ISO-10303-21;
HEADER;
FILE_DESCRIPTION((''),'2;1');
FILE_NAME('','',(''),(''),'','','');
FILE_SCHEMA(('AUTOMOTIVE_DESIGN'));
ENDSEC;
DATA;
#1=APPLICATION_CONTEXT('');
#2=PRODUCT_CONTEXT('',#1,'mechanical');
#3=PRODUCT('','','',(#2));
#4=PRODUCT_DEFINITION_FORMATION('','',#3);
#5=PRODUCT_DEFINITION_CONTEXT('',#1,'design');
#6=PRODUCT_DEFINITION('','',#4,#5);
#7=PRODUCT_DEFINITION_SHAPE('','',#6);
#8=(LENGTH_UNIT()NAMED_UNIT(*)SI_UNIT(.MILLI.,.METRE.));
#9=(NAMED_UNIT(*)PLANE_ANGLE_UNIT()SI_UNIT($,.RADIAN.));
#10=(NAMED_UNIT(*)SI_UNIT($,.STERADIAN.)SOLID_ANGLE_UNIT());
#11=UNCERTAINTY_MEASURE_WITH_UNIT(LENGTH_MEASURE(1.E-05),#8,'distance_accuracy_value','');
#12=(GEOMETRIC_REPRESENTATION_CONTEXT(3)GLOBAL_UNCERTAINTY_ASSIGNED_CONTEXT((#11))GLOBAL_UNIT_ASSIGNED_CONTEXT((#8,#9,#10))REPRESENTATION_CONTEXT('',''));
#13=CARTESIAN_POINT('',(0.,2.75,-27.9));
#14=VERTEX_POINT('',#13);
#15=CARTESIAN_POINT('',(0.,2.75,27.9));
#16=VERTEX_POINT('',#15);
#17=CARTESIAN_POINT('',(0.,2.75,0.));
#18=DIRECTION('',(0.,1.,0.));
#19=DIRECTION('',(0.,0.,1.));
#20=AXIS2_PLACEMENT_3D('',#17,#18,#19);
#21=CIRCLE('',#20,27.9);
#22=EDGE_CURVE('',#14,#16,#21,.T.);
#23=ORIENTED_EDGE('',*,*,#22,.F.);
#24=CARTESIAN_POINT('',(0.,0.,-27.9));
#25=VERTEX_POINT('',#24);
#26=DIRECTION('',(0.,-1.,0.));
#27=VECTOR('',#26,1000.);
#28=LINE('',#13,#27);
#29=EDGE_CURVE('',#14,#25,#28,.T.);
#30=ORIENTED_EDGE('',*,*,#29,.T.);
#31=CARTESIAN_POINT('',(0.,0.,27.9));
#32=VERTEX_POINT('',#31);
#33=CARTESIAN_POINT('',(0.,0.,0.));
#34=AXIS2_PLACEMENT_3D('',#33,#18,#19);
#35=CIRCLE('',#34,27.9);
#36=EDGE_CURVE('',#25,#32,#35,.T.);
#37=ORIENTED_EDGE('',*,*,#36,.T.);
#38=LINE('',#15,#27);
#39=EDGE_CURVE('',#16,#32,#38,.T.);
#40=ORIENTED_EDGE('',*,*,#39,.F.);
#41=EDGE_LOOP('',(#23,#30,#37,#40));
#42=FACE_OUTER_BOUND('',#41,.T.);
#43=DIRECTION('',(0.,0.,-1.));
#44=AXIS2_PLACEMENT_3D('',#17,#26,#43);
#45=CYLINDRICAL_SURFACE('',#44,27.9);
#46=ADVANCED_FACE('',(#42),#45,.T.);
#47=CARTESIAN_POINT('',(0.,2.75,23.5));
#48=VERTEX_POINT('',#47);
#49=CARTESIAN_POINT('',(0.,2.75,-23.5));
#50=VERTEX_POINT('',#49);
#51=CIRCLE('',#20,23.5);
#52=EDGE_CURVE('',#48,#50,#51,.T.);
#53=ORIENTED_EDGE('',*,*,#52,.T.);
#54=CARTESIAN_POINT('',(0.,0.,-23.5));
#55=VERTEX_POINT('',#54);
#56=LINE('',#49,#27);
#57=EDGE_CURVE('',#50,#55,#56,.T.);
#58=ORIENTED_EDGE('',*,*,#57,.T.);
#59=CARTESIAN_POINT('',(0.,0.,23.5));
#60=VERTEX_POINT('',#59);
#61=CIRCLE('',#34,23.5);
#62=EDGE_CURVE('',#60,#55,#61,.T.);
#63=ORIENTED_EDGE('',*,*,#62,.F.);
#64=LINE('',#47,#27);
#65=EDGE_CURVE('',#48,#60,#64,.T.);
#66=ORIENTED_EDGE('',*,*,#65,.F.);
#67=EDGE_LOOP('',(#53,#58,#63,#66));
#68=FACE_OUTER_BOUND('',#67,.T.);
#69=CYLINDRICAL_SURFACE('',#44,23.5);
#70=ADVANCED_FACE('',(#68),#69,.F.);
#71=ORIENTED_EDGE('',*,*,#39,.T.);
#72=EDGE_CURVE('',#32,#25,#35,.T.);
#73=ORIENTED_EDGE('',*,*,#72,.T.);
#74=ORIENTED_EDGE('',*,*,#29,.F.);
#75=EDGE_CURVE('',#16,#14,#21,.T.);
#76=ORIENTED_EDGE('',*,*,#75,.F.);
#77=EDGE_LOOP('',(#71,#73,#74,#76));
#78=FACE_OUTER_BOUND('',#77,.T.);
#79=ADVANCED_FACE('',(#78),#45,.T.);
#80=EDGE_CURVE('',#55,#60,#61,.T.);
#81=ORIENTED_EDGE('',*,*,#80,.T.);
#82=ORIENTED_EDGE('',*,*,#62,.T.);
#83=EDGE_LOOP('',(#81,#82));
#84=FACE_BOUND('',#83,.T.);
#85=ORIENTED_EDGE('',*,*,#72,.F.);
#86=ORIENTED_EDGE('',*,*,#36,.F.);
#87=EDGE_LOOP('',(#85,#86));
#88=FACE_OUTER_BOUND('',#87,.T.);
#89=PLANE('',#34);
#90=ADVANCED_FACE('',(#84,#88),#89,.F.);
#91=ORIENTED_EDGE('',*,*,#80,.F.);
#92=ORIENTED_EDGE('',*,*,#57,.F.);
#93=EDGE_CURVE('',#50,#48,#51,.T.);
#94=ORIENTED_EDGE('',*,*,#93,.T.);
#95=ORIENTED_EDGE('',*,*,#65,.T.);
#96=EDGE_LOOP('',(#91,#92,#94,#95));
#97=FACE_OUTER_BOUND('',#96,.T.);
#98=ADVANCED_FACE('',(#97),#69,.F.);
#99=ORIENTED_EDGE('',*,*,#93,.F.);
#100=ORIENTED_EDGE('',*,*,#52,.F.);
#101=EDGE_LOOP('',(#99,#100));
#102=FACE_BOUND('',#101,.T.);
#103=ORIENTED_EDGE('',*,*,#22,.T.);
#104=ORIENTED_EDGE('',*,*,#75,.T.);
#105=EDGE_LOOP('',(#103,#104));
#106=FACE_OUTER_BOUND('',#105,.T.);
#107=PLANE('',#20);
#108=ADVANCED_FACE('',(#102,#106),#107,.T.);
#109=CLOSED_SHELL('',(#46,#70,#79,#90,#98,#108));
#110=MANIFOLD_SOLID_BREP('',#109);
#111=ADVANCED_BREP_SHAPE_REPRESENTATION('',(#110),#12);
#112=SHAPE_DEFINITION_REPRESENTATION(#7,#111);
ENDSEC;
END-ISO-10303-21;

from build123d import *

# Parameters (mm, degrees)
SKETCH1_R           = 27.9
SKETCH1_R_2         = 23.5
BOSS_EXTRUDE1_DEPTH = 2.75


with BuildPart() as part:
    # Sketch1 → Boss-Extrude1 (new body)
    with BuildSketch(Plane(origin=(0, 0, 0), x_dir=(1, 0, 0), z_dir=(0, 1, 0))):
        with Locations(Location((0, 0, 0), (0, 0, 270))):
            Circle(SKETCH1_R)
        with Locations(Location((0, 0, 0), (0, 0, 270))):
            Circle(SKETCH1_R_2, mode=Mode.SUBTRACT)
    extrude(amount=BOSS_EXTRUDE1_DEPTH)


solid = part.part
